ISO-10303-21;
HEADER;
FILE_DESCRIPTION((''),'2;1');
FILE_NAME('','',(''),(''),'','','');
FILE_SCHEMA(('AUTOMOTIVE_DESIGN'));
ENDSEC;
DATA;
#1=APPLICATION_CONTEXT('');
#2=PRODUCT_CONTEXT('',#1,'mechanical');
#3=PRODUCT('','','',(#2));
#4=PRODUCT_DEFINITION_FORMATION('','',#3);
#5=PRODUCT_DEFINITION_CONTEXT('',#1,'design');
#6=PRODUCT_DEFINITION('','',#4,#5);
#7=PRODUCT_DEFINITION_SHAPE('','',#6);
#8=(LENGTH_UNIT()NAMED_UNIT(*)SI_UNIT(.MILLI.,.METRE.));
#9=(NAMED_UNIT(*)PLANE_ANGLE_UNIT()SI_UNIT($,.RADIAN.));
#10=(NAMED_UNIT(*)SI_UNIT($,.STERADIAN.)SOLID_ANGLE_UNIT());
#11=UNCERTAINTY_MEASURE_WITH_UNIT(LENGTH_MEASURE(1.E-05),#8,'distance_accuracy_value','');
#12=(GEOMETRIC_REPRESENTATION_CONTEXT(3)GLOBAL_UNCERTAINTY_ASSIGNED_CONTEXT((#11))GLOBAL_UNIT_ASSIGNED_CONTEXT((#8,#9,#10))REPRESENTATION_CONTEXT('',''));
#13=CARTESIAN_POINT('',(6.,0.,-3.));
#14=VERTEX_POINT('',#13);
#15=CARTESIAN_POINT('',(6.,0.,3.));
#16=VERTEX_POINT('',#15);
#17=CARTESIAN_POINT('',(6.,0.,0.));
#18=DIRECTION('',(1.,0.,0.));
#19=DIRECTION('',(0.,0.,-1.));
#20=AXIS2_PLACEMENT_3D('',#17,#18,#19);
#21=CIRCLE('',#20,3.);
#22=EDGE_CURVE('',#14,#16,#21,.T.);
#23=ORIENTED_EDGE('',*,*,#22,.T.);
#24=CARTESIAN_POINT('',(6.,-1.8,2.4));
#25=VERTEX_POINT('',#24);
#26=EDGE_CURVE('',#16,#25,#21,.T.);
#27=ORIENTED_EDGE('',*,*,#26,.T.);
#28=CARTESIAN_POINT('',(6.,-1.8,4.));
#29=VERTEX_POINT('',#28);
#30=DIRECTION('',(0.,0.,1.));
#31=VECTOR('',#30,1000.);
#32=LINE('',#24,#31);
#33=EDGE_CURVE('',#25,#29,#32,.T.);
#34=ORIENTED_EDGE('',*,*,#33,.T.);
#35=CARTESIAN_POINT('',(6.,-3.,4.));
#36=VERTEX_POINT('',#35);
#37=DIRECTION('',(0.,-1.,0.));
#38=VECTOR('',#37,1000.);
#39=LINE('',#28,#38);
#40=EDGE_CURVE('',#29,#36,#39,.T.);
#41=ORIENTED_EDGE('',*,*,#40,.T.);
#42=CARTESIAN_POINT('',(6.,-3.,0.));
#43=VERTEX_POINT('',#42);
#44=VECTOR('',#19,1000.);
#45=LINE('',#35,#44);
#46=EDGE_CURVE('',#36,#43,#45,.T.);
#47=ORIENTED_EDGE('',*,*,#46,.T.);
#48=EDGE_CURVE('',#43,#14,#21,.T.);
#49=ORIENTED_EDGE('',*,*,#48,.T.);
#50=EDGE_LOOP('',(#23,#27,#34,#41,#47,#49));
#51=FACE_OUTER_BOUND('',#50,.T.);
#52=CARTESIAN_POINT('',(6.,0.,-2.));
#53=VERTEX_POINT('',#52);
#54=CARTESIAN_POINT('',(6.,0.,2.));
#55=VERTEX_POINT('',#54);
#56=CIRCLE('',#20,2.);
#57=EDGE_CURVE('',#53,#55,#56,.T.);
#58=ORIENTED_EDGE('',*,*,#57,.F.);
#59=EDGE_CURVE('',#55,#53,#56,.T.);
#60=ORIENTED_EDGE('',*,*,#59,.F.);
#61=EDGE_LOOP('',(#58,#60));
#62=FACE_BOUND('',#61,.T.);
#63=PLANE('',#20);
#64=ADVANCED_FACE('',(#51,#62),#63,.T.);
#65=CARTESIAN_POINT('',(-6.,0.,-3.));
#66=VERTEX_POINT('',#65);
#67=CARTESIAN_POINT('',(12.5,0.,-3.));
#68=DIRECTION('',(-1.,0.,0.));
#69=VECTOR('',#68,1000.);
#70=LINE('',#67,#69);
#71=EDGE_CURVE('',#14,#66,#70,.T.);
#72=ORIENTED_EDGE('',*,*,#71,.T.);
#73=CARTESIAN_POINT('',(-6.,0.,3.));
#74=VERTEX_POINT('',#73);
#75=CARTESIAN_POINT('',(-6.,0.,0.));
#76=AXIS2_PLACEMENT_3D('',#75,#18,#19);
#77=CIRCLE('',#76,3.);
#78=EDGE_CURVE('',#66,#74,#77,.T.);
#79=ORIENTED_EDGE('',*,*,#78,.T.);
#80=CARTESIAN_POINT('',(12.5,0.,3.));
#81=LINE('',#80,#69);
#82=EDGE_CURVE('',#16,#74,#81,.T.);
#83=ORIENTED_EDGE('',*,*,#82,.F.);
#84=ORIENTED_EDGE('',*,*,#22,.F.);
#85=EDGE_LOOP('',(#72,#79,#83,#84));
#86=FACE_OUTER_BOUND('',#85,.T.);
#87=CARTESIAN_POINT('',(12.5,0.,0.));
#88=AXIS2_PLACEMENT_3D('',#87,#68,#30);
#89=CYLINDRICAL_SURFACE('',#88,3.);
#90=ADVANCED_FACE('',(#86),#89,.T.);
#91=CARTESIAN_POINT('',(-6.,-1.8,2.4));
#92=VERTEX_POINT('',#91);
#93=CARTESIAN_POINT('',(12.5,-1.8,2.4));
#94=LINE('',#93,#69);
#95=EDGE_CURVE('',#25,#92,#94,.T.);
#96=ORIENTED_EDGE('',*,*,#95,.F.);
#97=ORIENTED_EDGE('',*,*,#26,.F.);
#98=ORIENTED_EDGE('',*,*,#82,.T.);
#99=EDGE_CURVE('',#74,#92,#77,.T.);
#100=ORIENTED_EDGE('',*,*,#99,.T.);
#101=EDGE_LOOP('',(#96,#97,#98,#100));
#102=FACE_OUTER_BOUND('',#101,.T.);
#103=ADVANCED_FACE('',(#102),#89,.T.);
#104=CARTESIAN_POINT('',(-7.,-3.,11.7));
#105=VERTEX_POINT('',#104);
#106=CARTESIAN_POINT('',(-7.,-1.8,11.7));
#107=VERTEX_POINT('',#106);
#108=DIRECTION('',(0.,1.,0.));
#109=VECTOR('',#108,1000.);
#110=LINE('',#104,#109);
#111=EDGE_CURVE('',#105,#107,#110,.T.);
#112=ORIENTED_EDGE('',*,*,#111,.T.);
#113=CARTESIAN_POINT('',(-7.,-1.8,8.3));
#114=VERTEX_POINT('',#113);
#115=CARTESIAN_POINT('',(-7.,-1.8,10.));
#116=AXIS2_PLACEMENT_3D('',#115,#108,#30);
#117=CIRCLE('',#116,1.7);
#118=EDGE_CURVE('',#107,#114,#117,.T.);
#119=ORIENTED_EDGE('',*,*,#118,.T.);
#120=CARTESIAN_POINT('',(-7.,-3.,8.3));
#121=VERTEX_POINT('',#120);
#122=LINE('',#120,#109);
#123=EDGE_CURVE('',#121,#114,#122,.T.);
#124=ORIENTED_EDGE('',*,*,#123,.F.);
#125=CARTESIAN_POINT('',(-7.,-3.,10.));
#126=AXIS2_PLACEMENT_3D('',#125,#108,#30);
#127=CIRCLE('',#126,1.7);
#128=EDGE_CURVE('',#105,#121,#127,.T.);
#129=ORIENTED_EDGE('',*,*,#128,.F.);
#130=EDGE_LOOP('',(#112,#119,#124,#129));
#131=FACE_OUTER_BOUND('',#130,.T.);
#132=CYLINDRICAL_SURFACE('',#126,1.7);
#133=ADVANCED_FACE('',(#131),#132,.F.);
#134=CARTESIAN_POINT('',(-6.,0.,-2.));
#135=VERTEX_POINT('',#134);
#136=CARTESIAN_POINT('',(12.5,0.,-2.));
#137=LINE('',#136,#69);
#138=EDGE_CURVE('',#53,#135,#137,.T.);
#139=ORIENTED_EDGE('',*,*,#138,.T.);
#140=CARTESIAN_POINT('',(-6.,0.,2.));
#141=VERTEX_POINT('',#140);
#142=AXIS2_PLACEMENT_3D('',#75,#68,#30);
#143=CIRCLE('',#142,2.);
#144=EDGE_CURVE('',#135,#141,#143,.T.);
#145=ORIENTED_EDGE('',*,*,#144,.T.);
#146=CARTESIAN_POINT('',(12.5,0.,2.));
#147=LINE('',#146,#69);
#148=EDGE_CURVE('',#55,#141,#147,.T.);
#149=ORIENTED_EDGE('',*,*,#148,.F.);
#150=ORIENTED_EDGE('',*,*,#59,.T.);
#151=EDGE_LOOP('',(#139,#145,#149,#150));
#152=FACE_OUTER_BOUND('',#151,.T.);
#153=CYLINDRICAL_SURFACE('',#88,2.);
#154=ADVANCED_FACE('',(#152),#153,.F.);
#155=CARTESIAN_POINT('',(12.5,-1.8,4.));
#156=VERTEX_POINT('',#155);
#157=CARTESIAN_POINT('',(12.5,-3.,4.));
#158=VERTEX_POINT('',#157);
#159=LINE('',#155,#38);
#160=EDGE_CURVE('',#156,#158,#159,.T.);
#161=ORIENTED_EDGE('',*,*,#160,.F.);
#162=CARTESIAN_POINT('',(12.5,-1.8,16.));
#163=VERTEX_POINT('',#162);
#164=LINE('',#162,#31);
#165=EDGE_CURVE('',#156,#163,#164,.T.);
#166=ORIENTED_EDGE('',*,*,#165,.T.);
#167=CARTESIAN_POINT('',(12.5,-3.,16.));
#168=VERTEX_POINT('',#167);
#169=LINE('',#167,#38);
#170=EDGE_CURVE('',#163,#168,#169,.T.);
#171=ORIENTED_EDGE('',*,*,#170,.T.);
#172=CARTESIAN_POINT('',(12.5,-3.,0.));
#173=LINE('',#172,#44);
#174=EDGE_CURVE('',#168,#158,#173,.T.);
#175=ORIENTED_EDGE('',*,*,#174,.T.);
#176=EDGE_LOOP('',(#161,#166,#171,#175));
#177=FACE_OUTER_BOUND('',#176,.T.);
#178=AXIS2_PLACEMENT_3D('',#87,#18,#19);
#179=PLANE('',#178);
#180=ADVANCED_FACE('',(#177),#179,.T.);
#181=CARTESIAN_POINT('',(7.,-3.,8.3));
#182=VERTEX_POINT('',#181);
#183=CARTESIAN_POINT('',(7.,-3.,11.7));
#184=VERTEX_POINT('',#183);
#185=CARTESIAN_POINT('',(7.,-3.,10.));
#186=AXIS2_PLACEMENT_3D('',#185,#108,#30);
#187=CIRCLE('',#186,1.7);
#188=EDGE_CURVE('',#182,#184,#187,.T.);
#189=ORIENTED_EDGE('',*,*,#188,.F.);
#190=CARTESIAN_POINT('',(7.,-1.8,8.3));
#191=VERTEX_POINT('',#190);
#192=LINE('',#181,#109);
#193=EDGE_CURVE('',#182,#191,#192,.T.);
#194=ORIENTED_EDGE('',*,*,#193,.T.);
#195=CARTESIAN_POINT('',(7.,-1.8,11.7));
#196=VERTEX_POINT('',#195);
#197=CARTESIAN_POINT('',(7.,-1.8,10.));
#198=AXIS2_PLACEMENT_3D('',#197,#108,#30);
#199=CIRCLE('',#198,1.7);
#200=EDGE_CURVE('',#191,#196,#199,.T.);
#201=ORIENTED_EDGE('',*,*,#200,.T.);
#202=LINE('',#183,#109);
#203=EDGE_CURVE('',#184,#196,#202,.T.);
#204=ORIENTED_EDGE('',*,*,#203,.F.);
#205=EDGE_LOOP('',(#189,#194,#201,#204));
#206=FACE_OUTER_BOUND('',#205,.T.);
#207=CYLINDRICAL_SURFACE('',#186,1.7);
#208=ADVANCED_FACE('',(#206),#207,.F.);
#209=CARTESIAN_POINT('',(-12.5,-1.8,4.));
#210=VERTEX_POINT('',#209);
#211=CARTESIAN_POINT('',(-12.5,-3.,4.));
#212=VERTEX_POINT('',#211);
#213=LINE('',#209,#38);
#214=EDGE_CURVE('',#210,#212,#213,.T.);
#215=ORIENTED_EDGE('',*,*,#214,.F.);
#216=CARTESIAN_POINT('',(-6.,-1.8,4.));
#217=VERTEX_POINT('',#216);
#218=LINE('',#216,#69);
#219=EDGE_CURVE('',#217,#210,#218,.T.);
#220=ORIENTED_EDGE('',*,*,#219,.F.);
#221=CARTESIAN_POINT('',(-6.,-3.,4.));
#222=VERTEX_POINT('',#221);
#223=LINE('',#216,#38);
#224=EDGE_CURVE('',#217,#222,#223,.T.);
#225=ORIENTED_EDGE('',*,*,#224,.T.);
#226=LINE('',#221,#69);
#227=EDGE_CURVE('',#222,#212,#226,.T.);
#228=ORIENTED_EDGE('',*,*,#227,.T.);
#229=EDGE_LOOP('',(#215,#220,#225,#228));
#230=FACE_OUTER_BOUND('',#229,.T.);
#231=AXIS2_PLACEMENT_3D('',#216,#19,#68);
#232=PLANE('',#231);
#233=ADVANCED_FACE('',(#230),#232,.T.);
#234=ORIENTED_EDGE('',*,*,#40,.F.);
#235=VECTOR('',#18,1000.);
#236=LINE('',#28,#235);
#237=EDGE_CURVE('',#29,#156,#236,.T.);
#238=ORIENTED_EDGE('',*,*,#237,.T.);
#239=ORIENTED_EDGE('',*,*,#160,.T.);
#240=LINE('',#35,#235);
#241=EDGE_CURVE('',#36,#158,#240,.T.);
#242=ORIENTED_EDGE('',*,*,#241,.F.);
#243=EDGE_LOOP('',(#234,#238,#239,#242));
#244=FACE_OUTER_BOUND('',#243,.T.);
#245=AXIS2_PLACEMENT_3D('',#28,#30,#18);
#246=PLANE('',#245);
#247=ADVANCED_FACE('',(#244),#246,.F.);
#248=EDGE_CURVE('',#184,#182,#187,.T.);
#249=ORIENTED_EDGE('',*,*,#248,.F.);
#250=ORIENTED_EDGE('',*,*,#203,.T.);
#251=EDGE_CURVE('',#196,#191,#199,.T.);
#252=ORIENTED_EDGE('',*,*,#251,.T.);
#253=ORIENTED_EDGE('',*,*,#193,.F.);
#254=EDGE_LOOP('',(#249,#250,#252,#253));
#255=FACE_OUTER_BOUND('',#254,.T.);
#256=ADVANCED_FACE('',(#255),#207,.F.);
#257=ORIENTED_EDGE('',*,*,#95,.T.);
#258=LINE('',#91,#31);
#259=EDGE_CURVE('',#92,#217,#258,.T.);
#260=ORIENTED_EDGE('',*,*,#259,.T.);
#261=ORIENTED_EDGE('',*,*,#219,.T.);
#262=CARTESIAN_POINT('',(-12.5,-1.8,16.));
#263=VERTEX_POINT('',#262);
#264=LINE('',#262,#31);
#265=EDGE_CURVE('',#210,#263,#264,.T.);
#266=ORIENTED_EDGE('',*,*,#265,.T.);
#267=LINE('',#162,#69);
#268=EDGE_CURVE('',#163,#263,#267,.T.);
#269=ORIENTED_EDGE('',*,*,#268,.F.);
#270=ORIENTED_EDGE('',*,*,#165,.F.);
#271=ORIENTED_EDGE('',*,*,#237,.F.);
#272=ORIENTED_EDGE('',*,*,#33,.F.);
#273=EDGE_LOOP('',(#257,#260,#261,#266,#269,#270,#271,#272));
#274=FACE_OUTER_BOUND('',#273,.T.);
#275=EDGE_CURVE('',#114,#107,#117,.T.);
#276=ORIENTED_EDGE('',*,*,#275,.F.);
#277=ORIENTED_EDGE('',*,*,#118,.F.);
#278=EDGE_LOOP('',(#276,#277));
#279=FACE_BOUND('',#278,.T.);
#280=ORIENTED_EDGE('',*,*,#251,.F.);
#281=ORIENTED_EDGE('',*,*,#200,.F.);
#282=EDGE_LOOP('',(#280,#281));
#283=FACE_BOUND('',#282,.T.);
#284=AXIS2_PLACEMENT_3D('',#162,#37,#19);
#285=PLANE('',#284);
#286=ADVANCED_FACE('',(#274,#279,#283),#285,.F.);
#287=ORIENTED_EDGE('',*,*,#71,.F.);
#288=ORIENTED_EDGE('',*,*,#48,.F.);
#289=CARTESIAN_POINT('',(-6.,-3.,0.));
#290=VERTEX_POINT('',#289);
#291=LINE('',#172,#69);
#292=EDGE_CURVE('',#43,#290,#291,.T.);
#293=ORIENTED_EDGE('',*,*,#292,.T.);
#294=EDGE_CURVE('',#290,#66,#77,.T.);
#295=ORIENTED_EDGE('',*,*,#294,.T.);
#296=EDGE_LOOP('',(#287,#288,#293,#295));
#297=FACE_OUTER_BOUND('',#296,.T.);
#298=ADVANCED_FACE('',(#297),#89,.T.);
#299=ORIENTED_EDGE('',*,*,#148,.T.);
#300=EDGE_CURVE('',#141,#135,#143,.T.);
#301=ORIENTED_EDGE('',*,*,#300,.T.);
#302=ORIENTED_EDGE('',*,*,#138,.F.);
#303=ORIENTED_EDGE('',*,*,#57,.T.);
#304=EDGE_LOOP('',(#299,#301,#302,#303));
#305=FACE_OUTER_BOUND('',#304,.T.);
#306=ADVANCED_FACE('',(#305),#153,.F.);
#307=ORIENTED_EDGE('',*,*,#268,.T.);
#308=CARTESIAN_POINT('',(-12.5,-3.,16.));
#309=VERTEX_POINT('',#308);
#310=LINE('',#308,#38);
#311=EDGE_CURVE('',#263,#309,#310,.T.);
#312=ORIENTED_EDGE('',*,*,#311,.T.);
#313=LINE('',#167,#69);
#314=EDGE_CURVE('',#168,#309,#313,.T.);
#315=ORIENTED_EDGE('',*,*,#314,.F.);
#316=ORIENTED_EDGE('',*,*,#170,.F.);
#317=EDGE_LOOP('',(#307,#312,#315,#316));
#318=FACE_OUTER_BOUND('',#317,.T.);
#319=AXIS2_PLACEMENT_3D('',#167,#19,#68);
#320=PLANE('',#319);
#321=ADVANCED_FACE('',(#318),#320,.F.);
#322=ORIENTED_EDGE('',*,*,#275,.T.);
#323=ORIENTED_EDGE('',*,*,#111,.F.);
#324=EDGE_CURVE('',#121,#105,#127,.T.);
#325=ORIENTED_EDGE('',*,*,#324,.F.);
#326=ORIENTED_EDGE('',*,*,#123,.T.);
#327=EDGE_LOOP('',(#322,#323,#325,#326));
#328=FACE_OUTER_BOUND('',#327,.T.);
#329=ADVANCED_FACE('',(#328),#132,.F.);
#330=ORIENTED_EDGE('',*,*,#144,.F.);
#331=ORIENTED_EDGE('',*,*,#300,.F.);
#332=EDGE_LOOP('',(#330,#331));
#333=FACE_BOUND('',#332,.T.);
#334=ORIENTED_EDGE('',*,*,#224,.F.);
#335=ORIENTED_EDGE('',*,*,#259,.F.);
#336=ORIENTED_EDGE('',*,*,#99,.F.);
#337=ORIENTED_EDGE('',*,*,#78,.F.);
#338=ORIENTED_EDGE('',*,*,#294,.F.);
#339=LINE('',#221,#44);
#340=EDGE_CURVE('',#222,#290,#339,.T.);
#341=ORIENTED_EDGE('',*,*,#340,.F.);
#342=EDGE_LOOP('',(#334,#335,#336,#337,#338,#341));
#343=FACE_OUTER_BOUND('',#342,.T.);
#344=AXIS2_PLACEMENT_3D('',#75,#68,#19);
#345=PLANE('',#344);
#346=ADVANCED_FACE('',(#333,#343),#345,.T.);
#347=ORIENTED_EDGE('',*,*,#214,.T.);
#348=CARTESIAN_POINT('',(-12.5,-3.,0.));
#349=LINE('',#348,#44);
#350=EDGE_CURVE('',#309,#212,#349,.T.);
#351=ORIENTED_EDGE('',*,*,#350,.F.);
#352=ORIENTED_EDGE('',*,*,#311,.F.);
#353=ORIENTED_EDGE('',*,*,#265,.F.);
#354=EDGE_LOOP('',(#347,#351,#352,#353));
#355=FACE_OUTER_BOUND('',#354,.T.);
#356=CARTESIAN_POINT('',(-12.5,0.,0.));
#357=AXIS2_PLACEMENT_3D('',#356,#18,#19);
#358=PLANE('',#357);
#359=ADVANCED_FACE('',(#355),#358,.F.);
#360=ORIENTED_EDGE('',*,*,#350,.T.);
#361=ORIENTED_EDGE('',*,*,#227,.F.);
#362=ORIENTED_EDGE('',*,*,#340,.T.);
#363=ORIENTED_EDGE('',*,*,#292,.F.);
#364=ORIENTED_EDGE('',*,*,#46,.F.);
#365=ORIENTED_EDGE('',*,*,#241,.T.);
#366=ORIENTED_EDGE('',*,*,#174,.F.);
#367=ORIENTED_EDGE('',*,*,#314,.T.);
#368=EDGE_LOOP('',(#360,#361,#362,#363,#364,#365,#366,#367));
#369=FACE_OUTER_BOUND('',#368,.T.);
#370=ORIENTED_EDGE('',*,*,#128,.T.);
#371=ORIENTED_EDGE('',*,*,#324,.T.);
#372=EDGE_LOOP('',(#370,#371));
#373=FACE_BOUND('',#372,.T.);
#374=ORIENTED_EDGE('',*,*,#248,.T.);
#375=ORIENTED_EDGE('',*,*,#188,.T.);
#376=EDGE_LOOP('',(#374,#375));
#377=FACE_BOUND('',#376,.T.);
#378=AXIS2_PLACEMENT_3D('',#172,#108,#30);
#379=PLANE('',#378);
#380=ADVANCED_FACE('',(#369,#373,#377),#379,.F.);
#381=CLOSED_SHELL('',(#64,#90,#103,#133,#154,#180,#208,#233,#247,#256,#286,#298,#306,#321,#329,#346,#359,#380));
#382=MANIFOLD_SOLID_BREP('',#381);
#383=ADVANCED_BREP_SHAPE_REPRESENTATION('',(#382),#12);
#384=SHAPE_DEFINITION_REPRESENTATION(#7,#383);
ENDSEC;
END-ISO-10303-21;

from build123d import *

# Parameters (mm, degrees)
SKETCH_1_R          = 2
EXTRUDE_1_DEPTH     = 12.5
SKETCH_2_R          = 1.7
CUT_EXTRUDE_1_DEPTH = 21.863604674
CUT_EXTRUDE_2_DEPTH = 6.5


with BuildPart() as part:
    # 草图1 → 凸台-拉伸1 (new, symmetric)
    with BuildSketch(Plane(origin=(0, 0, 0), x_dir=(0, 0, -1), z_dir=(1, 0, 0))):
        with BuildLine():
            Line((0, -3), (-16, -3))
            Line((-16, -3), (-16, -1.8))
            Line((-16, -1.8), (-2.4, -1.8))
            ThreePointArc((-2.4, -1.8), (1.341640786, 2.683281573), (0, -3))
        make_face()
        Circle(SKETCH_1_R, mode=Mode.SUBTRACT)
    extrude(amount=EXTRUDE_1_DEPTH, both=True)

    # 草图2 → 切除-拉伸1 (cut, through all)
    with BuildSketch(Plane(origin=(0, -1.8, 0), x_dir=(1, 0, 0), z_dir=(0, 1, 0))):
        with Locations(Location((-7, -10, 0), (0, 0, 270))):
            Circle(SKETCH_2_R)
        with Locations(Location((7, -10, 0), (0, 0, 270))):
            Circle(SKETCH_2_R)
    extrude(amount=-CUT_EXTRUDE_1_DEPTH, mode=Mode.SUBTRACT)

    # 草图3 → 切除-拉伸2 (cut)
    with BuildSketch(Plane(origin=(12.5, 0, 0), x_dir=(0, 0, -1), z_dir=(1, 0, 0))):
        with BuildLine():
            Line((-4, -3), (0, -3))
            ThreePointArc((0, -3), (1.341640786, 2.683281573), (-2.4, -1.8))
            Line((-2.4, -1.8), (-4, -1.8))
            Line((-4, -1.8), (-4, -3))
        make_face()
    cut_extrude_2 = extrude(amount=-CUT_EXTRUDE_2_DEPTH, mode=Mode.SUBTRACT)

    # 镜向1: 切除-拉伸2 across plane
    add(cut_extrude_2.mirror(Plane(origin=(0, 0, 0), x_dir=(0, 0, 1), z_dir=(1, 0, 0))), mode=Mode.SUBTRACT)


solid = part.part
